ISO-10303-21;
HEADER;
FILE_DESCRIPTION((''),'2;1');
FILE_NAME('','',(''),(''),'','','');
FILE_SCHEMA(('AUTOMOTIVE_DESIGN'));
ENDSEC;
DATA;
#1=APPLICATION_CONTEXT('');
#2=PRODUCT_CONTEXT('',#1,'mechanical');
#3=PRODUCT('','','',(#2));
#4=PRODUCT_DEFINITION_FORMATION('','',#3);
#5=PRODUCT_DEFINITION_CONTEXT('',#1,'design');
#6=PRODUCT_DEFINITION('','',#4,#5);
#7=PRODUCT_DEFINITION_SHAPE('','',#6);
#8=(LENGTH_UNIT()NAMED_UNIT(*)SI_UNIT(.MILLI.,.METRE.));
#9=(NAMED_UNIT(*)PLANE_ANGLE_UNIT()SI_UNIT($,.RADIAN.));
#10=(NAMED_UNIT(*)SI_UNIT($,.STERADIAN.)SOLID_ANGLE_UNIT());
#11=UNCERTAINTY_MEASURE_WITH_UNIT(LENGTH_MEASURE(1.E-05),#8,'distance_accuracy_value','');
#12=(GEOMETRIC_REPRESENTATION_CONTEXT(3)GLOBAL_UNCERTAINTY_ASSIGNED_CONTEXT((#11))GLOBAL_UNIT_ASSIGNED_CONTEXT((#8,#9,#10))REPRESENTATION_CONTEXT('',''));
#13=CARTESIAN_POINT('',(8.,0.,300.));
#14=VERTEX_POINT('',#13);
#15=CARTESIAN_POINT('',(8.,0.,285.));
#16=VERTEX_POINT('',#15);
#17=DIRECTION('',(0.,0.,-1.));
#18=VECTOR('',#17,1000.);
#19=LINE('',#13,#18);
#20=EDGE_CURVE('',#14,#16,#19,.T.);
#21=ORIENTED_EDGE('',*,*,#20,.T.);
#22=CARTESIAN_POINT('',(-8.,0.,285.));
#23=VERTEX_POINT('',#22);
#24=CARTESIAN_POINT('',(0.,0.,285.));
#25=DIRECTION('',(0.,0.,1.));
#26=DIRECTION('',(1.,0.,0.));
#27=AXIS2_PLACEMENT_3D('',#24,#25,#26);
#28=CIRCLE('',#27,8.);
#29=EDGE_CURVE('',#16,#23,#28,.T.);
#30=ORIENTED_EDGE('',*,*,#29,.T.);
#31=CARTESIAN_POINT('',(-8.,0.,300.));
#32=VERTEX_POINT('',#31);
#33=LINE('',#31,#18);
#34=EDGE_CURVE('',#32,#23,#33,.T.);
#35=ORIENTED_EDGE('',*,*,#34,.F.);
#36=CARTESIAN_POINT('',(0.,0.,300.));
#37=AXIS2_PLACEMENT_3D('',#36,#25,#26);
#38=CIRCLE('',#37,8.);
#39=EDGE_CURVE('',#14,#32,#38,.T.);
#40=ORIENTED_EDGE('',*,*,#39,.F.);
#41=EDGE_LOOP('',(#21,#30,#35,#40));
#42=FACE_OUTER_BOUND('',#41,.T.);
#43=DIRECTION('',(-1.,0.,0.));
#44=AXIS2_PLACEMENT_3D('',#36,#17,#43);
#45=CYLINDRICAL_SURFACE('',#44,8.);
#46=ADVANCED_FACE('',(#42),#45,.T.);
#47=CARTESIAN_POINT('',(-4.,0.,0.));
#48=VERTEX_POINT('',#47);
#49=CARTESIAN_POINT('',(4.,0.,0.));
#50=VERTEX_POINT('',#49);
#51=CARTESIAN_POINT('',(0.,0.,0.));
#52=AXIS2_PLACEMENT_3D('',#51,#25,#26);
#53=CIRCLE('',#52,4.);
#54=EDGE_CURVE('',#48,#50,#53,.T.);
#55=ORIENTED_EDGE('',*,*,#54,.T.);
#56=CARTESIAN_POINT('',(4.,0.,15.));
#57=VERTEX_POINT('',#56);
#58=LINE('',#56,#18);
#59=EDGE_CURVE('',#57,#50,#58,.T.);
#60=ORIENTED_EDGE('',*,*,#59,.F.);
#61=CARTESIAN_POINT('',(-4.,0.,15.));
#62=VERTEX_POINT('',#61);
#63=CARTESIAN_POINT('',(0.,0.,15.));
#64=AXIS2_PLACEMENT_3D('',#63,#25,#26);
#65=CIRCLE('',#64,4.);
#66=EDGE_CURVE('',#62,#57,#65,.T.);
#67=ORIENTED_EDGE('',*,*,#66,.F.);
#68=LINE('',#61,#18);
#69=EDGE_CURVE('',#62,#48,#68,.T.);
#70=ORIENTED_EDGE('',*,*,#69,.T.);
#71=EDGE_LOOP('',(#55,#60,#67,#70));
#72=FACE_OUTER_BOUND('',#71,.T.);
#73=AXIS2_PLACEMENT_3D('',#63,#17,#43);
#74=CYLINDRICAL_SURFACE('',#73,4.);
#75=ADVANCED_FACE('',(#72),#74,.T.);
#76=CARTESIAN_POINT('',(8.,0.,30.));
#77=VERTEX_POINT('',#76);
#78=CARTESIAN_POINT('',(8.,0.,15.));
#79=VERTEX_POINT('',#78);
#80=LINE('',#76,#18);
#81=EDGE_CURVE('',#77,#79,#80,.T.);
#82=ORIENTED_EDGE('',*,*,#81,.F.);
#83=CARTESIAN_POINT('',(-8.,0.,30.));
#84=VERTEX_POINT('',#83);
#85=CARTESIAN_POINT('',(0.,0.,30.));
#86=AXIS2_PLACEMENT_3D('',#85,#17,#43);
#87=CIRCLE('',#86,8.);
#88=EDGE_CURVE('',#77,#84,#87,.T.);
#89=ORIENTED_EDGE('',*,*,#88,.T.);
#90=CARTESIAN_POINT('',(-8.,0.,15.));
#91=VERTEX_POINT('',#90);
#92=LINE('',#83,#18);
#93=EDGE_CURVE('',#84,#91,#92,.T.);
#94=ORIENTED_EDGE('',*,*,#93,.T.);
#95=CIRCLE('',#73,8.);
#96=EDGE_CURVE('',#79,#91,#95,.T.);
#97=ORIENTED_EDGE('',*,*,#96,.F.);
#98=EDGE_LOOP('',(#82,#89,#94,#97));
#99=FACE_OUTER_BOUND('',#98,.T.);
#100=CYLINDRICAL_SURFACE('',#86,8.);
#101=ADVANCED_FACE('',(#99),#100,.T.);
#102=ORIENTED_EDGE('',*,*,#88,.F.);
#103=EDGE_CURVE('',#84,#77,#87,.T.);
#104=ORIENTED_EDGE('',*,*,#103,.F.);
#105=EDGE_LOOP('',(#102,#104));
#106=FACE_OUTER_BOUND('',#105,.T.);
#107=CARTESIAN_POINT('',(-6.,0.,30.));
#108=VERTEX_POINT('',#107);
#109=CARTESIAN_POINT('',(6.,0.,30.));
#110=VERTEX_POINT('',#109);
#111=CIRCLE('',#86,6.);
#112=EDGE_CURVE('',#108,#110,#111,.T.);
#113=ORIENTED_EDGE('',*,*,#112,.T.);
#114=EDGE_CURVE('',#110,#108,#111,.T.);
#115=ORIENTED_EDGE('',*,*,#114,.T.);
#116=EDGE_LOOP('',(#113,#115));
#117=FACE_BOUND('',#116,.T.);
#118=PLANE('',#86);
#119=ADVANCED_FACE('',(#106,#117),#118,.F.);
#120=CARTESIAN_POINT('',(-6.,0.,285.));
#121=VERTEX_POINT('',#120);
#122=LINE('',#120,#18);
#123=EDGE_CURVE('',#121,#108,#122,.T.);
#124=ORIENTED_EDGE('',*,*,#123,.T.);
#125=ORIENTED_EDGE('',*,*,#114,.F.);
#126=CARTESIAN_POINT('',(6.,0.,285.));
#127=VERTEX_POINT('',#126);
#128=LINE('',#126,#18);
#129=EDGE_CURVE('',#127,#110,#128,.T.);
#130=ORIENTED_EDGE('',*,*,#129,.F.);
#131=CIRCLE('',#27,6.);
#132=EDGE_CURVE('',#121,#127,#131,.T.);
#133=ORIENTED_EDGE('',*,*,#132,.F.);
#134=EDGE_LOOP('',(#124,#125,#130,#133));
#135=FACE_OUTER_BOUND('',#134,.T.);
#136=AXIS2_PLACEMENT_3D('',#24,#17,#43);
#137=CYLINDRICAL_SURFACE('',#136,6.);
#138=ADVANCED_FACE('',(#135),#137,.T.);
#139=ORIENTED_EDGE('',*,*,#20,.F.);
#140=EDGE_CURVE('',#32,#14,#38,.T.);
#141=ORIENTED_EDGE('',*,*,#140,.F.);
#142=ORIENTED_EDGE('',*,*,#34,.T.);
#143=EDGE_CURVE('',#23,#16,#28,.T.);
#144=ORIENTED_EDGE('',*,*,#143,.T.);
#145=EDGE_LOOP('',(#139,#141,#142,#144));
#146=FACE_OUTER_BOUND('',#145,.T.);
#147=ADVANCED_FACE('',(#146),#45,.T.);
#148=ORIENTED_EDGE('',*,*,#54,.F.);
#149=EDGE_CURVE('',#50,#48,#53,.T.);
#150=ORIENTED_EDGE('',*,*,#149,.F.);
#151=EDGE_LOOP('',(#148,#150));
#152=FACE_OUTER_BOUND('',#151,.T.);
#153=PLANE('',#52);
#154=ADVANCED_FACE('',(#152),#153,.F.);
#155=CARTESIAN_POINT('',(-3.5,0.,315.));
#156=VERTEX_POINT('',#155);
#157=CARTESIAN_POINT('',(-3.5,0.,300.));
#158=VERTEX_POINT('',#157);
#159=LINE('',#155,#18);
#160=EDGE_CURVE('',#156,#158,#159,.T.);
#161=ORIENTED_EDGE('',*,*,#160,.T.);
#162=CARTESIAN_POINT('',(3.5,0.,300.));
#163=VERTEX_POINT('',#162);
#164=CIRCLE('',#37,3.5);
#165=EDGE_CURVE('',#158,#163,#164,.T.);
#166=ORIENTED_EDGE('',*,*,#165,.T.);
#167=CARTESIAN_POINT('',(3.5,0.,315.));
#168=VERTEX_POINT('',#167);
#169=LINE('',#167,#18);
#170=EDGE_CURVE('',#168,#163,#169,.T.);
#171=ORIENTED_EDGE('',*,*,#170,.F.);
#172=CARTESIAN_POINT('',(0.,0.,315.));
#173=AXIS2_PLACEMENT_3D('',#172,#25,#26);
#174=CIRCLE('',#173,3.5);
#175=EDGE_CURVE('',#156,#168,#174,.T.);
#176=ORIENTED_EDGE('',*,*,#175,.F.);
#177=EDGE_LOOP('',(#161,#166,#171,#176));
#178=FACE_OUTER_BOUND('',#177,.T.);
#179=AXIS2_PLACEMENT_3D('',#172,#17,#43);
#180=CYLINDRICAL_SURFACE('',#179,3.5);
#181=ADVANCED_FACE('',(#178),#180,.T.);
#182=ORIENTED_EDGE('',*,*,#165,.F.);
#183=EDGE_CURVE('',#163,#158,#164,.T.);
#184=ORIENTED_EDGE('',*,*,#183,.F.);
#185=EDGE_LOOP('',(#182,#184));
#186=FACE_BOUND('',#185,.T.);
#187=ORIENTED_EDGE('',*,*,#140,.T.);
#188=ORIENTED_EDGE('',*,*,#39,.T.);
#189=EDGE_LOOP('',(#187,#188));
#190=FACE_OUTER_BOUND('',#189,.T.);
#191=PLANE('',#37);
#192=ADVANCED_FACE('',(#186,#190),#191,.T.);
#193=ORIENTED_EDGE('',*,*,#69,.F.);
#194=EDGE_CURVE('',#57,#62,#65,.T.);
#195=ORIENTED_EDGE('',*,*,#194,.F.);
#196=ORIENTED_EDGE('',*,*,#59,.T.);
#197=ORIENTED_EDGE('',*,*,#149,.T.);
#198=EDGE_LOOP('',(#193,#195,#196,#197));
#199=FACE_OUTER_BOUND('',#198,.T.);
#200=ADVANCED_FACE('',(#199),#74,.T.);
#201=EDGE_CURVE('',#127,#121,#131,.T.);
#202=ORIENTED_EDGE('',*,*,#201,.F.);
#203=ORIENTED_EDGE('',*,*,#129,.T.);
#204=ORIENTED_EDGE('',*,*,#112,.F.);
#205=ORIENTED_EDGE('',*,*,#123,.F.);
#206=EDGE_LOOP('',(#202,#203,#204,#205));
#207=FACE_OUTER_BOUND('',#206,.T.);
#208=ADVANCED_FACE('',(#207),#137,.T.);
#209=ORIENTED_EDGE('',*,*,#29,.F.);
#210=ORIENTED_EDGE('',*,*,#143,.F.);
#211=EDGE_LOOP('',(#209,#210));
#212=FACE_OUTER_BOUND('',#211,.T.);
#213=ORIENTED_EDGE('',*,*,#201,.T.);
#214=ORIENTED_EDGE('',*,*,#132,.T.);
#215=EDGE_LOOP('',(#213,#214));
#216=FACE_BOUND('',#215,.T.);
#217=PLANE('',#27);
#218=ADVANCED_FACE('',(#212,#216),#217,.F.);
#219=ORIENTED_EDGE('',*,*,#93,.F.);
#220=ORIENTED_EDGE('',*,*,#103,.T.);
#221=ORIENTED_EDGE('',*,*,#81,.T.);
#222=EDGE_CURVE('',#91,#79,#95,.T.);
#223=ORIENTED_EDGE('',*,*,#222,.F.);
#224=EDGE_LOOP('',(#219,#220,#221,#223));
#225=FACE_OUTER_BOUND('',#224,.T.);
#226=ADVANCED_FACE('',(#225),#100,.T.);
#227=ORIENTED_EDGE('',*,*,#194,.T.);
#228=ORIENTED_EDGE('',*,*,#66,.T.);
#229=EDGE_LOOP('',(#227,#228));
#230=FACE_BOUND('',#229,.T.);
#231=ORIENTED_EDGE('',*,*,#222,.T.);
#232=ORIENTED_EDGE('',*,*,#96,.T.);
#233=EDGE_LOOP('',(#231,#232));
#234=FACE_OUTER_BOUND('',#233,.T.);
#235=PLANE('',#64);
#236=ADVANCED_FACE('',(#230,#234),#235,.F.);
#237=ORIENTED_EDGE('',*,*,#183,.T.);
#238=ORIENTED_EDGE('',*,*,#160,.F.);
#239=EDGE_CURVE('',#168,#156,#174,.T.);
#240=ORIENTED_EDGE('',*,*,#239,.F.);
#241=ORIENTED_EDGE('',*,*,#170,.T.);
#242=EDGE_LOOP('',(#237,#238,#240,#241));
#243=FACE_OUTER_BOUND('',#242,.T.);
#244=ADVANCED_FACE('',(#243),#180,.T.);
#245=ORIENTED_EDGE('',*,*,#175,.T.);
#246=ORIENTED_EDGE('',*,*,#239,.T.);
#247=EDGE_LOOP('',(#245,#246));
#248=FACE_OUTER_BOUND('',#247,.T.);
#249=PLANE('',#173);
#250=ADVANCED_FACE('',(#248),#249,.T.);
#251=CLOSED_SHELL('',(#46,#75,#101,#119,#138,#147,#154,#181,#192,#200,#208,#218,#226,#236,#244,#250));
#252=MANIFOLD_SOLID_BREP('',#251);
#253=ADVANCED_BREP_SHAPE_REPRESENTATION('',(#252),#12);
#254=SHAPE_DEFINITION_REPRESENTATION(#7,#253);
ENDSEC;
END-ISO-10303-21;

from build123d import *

# Parameters (mm, degrees)
SKETCH_1_R      = 4
EXTRUDE_1_DEPTH = 15
SKETCH_2_R      = 6
EXTRUDE_2_DEPTH = 270
SKETCH_3_R      = 8
EXTRUDE_3_DEPTH = 15
SKETCH_4_R      = 8
EXTRUDE_4_DEPTH = 15
SKETCH_5_R      = 3.5
EXTRUDE_5_DEPTH = 15


with BuildPart() as part:
    # 草图1 → 凸台-拉伸1 (new body)
    with BuildSketch(Plane.XY):
        Circle(SKETCH_1_R)
    extrude(amount=EXTRUDE_1_DEPTH)

    # 草图2 → 凸台-拉伸2 (add)
    with BuildSketch(Plane.XY.offset(15)):
        Circle(SKETCH_2_R)
    extrude(amount=EXTRUDE_2_DEPTH)

    # 草图3 → 凸台-拉伸3 (add)
    with BuildSketch(Plane(origin=(0, 0, 15), x_dir=(-1, 0, 0), z_dir=(0, 0, -1))):
        Circle(SKETCH_3_R)
    extrude(amount=-EXTRUDE_3_DEPTH)

    # 草图4 → 凸台-拉伸4 (add)
    with BuildSketch(Plane.XY.offset(285)):
        with Locations(Location((0, 0, 0), (0, 0, 180))):
            Circle(SKETCH_4_R)
    extrude(amount=EXTRUDE_4_DEPTH)

    # 草图5 → 凸台-拉伸5 (add)
    with BuildSketch(Plane.XY.offset(300)):
        Circle(SKETCH_5_R)
    extrude(amount=EXTRUDE_5_DEPTH)


solid = part.part
